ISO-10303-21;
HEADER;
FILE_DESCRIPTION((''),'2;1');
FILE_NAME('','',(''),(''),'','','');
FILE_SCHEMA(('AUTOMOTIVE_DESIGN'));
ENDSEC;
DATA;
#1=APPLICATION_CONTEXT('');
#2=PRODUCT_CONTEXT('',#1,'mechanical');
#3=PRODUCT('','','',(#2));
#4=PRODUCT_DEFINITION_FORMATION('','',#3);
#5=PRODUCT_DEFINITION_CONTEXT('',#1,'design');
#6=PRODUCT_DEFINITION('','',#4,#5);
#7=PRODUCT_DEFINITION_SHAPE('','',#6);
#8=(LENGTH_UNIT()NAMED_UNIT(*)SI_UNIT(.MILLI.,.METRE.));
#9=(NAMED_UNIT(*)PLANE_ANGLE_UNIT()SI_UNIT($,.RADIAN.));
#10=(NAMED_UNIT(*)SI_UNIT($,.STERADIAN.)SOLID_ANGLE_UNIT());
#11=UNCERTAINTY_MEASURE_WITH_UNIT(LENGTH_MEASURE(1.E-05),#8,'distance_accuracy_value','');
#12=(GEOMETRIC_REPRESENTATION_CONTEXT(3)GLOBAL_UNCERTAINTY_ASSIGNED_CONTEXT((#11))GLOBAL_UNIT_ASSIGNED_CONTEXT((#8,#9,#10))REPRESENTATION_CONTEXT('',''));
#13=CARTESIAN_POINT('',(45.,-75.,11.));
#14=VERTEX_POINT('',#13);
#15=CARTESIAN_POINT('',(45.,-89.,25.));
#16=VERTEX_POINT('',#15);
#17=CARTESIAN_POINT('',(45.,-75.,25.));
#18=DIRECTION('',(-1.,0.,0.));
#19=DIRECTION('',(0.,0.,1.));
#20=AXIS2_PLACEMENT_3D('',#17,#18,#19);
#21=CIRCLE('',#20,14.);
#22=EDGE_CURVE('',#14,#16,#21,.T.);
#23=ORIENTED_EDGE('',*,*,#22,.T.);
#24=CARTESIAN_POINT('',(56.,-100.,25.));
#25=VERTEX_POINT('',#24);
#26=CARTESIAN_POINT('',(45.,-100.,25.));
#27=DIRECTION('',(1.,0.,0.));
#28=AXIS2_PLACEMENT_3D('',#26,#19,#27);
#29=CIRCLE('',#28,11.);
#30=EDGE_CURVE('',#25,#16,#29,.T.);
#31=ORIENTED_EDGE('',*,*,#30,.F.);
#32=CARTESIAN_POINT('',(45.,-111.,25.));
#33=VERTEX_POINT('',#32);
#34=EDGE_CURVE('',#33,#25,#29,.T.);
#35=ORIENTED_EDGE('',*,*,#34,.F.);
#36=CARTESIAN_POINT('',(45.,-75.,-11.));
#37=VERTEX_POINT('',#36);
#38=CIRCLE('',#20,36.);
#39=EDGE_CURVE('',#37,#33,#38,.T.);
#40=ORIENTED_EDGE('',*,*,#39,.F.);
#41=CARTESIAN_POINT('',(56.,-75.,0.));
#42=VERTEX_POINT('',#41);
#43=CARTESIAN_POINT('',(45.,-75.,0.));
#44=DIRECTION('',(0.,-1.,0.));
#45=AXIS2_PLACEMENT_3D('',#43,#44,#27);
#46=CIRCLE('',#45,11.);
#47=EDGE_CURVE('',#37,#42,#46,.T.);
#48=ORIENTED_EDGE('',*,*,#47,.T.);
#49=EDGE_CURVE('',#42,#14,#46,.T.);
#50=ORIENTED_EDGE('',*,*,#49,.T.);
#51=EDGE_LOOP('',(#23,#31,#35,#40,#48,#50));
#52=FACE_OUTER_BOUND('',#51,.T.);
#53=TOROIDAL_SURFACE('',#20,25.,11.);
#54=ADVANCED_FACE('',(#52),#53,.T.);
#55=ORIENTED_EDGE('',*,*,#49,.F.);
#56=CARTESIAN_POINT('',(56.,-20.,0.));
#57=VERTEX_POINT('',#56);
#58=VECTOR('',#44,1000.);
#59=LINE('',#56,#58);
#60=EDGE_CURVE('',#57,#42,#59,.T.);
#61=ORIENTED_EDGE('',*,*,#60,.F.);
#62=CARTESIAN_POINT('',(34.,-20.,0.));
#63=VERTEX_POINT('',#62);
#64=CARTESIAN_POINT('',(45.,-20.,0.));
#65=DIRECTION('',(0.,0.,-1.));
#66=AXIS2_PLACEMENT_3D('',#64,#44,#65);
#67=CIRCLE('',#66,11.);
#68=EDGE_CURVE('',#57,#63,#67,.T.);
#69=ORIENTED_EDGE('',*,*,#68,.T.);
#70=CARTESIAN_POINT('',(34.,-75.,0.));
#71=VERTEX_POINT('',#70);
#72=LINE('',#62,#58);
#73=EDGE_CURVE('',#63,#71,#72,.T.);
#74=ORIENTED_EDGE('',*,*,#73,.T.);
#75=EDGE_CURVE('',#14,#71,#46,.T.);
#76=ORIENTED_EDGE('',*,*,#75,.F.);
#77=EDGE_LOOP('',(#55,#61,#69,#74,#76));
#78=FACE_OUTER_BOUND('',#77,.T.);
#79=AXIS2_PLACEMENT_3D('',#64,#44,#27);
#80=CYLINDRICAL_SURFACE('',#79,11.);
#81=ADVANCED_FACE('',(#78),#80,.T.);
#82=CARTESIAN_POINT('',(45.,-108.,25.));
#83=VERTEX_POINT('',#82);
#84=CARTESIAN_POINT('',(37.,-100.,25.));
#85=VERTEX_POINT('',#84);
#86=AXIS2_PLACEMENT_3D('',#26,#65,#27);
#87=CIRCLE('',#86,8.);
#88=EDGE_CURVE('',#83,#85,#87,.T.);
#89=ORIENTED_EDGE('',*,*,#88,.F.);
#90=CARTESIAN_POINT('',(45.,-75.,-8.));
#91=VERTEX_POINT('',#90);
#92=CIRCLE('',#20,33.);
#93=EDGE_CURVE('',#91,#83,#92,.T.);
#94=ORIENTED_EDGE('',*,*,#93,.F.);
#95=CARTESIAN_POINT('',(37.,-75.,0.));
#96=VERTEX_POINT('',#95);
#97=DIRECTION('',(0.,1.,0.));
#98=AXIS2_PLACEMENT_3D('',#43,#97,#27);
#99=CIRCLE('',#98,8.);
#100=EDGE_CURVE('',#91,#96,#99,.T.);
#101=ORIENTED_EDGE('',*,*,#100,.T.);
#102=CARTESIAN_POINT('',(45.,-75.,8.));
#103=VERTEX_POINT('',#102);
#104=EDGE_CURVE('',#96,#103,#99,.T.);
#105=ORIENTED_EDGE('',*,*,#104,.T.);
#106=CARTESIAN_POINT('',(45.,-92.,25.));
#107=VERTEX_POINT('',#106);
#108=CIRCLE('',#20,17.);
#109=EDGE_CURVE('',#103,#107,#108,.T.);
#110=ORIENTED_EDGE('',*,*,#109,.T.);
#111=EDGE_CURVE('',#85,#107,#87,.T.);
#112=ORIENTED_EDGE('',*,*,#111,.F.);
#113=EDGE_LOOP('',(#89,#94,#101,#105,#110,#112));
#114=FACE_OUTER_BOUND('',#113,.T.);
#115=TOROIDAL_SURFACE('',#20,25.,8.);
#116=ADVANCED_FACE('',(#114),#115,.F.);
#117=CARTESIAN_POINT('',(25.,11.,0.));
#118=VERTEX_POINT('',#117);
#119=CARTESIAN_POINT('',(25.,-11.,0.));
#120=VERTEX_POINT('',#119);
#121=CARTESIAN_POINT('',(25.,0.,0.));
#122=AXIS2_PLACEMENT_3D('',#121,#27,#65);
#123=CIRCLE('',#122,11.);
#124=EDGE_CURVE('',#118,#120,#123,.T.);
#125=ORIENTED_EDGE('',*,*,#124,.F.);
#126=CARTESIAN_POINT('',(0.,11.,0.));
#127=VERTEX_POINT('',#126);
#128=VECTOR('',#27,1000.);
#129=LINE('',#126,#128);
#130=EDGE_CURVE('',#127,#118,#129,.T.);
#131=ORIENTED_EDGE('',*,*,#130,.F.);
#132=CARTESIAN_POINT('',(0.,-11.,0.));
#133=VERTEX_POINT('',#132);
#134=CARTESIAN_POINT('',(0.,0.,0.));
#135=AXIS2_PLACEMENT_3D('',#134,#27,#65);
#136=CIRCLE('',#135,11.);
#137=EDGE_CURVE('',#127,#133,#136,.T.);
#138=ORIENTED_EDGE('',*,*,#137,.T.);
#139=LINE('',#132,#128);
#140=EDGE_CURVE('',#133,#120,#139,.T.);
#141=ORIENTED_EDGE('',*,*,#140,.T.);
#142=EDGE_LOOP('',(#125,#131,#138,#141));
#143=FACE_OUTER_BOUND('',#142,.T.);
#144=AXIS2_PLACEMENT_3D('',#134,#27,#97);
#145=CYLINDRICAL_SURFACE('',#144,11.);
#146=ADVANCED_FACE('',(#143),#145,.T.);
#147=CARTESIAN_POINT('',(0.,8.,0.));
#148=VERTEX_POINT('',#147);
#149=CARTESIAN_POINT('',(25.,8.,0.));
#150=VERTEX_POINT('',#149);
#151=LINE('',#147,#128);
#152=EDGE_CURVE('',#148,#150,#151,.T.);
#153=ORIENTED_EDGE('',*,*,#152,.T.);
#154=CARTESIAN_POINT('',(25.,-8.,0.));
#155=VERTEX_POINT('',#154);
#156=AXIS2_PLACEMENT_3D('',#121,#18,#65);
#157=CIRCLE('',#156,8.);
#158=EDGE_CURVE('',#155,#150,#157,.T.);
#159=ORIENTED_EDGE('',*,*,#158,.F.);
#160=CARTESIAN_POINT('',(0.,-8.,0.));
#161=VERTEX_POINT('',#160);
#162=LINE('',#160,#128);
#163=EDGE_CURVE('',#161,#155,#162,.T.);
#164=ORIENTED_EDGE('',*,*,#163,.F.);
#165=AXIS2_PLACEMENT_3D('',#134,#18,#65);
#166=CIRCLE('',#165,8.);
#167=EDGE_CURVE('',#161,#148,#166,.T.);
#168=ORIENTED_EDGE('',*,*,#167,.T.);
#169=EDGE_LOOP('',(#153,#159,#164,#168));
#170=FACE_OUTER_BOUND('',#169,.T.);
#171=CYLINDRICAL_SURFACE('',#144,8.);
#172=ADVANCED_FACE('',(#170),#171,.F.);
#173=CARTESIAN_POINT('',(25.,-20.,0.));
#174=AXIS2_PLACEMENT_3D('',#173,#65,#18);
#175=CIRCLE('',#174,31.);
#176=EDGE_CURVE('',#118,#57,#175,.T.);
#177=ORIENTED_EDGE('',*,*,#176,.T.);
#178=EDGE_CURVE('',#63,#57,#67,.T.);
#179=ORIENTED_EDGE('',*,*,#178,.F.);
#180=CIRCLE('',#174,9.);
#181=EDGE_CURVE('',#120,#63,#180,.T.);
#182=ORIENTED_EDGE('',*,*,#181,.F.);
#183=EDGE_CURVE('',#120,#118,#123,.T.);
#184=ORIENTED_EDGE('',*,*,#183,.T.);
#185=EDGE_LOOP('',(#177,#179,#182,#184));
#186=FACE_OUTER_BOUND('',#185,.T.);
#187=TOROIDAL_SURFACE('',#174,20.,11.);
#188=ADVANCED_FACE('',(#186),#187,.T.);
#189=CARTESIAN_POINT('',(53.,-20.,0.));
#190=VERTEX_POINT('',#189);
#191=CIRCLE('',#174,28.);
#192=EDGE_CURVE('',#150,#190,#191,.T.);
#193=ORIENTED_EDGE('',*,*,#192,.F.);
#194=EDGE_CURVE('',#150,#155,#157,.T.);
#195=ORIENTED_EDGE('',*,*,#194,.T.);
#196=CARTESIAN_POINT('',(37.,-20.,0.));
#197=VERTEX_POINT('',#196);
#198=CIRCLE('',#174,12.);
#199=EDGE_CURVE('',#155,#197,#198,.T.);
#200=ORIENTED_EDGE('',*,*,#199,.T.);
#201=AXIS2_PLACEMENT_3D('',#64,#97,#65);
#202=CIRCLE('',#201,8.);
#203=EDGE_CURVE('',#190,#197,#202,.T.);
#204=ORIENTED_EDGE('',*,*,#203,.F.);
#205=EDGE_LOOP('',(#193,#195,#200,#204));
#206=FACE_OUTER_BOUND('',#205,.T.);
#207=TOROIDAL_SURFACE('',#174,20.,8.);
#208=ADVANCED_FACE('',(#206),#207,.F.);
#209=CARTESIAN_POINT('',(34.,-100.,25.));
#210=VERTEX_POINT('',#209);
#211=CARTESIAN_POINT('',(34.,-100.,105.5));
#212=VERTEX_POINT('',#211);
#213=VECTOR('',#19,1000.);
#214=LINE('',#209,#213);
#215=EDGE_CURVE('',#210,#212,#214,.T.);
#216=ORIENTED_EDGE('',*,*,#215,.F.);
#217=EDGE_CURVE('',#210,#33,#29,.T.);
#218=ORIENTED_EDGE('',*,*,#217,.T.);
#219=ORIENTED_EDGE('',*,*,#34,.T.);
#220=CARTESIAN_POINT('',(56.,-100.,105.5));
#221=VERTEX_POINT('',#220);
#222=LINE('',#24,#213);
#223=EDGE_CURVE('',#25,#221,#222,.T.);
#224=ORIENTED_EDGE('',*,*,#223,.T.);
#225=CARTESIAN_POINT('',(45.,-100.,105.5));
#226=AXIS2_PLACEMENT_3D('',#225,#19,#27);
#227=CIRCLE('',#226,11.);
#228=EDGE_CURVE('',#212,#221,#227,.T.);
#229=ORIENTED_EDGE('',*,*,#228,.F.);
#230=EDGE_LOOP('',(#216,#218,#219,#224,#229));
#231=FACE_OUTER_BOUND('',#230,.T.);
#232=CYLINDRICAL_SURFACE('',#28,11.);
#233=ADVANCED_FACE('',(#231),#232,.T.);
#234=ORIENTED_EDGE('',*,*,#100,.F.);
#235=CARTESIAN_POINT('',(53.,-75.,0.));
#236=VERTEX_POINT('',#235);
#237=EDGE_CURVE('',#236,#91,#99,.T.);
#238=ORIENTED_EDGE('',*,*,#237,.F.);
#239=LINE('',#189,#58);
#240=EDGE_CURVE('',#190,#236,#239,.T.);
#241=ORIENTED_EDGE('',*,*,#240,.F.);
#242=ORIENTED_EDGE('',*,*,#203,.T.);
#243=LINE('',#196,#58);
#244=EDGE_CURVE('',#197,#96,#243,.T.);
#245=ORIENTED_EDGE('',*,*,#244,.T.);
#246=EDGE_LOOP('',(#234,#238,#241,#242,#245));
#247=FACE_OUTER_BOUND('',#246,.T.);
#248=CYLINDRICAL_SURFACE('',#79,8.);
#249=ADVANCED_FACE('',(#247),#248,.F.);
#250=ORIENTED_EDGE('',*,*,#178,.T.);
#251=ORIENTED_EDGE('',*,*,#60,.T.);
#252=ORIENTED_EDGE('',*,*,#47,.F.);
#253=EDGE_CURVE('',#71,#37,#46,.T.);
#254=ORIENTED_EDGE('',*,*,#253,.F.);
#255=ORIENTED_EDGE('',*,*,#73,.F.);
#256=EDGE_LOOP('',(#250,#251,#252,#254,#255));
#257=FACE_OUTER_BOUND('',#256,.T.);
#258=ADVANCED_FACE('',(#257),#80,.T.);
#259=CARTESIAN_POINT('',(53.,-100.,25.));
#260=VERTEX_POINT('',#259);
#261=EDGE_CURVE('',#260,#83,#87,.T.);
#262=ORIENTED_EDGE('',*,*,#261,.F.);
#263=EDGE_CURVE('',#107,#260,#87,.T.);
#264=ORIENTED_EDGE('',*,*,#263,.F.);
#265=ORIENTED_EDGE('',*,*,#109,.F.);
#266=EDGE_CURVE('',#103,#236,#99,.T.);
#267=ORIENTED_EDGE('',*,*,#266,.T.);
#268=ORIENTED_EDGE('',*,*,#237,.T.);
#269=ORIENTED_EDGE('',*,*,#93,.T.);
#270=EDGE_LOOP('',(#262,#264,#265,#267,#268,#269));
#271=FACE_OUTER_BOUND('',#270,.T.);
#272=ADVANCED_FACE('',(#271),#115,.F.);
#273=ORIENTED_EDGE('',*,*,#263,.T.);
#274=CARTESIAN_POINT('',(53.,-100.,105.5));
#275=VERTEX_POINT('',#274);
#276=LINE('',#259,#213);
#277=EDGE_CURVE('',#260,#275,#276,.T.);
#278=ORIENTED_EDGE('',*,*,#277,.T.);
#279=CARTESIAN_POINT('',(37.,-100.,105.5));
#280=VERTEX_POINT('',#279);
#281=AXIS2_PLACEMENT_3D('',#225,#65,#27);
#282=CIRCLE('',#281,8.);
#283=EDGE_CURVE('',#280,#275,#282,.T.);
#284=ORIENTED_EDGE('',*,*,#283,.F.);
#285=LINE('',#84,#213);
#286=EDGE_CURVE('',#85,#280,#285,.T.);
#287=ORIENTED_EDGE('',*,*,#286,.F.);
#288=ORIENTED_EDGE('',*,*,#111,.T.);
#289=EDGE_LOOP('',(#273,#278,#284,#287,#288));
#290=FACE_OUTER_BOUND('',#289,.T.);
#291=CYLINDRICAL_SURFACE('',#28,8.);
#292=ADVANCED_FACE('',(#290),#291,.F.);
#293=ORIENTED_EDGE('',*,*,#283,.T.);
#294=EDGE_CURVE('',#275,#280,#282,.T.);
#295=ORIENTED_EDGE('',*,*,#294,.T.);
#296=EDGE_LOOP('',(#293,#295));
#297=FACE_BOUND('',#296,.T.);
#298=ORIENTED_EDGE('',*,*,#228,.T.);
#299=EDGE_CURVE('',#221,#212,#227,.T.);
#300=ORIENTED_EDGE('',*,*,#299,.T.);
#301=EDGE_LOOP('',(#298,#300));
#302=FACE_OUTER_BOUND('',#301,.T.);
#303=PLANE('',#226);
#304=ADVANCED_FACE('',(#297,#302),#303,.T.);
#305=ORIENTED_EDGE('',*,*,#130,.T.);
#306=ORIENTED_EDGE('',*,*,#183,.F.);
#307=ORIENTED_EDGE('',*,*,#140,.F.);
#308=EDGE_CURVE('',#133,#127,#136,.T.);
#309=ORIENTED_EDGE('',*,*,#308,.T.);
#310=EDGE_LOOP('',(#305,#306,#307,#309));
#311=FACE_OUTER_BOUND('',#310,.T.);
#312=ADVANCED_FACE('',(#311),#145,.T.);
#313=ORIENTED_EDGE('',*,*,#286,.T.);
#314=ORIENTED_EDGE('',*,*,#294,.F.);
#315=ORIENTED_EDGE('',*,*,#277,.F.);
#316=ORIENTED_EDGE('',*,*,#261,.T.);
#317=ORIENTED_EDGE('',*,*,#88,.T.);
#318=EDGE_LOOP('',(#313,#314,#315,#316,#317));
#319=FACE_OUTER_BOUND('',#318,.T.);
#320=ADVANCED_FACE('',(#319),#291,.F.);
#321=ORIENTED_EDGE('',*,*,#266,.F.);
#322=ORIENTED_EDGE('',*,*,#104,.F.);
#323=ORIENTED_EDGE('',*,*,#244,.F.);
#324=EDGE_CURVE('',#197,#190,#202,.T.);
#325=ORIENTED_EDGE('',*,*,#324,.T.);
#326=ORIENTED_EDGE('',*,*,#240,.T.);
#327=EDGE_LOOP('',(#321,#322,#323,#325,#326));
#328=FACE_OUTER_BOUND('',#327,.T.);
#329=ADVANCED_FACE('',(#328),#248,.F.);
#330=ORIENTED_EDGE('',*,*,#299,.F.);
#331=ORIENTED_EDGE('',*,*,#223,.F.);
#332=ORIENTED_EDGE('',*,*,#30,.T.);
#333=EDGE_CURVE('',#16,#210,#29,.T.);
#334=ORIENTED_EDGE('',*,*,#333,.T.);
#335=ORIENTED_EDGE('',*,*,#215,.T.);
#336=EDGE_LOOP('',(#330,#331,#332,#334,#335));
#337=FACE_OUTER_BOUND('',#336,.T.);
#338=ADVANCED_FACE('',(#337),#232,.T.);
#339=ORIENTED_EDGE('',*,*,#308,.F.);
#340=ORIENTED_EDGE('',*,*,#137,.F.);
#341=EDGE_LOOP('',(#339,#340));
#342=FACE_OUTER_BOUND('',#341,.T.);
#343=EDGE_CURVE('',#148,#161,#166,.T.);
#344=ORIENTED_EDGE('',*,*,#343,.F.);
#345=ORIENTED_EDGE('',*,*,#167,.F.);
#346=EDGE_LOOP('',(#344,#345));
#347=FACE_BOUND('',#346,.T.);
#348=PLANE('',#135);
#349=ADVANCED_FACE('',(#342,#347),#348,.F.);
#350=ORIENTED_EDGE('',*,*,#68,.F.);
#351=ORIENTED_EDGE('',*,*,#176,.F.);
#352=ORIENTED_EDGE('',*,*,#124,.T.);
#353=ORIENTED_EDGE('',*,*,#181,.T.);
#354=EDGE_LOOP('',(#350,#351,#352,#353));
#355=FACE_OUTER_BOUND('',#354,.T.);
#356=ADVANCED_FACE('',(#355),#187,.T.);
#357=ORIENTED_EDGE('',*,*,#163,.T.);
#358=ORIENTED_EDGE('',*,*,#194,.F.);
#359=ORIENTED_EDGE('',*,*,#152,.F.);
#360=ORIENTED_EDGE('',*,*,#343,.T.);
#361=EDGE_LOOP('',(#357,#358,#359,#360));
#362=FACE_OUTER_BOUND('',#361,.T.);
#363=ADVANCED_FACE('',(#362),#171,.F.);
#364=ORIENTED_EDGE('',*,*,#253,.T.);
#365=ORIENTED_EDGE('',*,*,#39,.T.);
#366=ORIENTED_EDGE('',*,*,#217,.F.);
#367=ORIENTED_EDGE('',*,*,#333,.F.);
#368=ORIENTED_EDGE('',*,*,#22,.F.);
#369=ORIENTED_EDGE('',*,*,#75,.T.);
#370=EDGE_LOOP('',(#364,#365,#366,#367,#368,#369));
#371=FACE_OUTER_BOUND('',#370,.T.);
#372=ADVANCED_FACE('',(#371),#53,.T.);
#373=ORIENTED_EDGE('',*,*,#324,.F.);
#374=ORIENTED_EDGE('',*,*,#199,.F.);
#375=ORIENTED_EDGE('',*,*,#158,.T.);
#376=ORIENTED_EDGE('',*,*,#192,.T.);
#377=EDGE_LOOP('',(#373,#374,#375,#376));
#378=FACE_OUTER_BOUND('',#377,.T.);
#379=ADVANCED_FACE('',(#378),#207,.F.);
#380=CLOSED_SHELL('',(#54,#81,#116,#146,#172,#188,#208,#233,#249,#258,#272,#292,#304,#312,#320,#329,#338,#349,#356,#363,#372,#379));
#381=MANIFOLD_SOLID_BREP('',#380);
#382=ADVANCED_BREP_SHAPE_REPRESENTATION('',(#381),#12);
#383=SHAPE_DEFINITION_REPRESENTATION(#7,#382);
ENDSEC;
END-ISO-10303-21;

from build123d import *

# Parameters (mm, degrees)
SKETCH_2_R   = 11
SKETCH_2_R_2 = 8
SKETCH_4_R   = 11
SKETCH_4_R_2 = 8


with BuildPart() as part:
    # Sweep 1: sweep along a path in Sketch 1
    with BuildLine(Plane.XY) as sweep_1_path:
        Line((0, 0), (25, 0))
        ThreePointArc((25, 0), (39.142135624, -5.857864376), (45, -20))
        Line((45, -20), (45, -50))
    # Sketch 2 → Sweep 1 (sweep)
    with BuildSketch(Plane(origin=(0, 0, 0), x_dir=(0, 0, -1), z_dir=(1, 0, 0))):
        Circle(SKETCH_2_R)
        Circle(SKETCH_2_R_2, mode=Mode.SUBTRACT)
    sweep(path=sweep_1_path.line)

    # Sweep 2: sweep along a path in Sketch 3
    with BuildLine(Plane(origin=(45, 0, 0), x_dir=(0, 0, -1), z_dir=(1, 0, 0))) as sweep_2_path:
        Line((0, -50), (0, -75))
        ThreePointArc((0, -75), (-7.32233047, -92.67766953), (-25, -100))
        Line((-25, -100), (-105.5, -100))
    # Sketch 4 → Sweep 2 (sweep)
    with BuildSketch(Plane.XZ.offset(50)):
        with Locations((45, 0)):
            Circle(SKETCH_4_R)
        with Locations((45, 0)):
            Circle(SKETCH_4_R_2, mode=Mode.SUBTRACT)
    sweep(path=sweep_2_path.line)


solid = part.part
